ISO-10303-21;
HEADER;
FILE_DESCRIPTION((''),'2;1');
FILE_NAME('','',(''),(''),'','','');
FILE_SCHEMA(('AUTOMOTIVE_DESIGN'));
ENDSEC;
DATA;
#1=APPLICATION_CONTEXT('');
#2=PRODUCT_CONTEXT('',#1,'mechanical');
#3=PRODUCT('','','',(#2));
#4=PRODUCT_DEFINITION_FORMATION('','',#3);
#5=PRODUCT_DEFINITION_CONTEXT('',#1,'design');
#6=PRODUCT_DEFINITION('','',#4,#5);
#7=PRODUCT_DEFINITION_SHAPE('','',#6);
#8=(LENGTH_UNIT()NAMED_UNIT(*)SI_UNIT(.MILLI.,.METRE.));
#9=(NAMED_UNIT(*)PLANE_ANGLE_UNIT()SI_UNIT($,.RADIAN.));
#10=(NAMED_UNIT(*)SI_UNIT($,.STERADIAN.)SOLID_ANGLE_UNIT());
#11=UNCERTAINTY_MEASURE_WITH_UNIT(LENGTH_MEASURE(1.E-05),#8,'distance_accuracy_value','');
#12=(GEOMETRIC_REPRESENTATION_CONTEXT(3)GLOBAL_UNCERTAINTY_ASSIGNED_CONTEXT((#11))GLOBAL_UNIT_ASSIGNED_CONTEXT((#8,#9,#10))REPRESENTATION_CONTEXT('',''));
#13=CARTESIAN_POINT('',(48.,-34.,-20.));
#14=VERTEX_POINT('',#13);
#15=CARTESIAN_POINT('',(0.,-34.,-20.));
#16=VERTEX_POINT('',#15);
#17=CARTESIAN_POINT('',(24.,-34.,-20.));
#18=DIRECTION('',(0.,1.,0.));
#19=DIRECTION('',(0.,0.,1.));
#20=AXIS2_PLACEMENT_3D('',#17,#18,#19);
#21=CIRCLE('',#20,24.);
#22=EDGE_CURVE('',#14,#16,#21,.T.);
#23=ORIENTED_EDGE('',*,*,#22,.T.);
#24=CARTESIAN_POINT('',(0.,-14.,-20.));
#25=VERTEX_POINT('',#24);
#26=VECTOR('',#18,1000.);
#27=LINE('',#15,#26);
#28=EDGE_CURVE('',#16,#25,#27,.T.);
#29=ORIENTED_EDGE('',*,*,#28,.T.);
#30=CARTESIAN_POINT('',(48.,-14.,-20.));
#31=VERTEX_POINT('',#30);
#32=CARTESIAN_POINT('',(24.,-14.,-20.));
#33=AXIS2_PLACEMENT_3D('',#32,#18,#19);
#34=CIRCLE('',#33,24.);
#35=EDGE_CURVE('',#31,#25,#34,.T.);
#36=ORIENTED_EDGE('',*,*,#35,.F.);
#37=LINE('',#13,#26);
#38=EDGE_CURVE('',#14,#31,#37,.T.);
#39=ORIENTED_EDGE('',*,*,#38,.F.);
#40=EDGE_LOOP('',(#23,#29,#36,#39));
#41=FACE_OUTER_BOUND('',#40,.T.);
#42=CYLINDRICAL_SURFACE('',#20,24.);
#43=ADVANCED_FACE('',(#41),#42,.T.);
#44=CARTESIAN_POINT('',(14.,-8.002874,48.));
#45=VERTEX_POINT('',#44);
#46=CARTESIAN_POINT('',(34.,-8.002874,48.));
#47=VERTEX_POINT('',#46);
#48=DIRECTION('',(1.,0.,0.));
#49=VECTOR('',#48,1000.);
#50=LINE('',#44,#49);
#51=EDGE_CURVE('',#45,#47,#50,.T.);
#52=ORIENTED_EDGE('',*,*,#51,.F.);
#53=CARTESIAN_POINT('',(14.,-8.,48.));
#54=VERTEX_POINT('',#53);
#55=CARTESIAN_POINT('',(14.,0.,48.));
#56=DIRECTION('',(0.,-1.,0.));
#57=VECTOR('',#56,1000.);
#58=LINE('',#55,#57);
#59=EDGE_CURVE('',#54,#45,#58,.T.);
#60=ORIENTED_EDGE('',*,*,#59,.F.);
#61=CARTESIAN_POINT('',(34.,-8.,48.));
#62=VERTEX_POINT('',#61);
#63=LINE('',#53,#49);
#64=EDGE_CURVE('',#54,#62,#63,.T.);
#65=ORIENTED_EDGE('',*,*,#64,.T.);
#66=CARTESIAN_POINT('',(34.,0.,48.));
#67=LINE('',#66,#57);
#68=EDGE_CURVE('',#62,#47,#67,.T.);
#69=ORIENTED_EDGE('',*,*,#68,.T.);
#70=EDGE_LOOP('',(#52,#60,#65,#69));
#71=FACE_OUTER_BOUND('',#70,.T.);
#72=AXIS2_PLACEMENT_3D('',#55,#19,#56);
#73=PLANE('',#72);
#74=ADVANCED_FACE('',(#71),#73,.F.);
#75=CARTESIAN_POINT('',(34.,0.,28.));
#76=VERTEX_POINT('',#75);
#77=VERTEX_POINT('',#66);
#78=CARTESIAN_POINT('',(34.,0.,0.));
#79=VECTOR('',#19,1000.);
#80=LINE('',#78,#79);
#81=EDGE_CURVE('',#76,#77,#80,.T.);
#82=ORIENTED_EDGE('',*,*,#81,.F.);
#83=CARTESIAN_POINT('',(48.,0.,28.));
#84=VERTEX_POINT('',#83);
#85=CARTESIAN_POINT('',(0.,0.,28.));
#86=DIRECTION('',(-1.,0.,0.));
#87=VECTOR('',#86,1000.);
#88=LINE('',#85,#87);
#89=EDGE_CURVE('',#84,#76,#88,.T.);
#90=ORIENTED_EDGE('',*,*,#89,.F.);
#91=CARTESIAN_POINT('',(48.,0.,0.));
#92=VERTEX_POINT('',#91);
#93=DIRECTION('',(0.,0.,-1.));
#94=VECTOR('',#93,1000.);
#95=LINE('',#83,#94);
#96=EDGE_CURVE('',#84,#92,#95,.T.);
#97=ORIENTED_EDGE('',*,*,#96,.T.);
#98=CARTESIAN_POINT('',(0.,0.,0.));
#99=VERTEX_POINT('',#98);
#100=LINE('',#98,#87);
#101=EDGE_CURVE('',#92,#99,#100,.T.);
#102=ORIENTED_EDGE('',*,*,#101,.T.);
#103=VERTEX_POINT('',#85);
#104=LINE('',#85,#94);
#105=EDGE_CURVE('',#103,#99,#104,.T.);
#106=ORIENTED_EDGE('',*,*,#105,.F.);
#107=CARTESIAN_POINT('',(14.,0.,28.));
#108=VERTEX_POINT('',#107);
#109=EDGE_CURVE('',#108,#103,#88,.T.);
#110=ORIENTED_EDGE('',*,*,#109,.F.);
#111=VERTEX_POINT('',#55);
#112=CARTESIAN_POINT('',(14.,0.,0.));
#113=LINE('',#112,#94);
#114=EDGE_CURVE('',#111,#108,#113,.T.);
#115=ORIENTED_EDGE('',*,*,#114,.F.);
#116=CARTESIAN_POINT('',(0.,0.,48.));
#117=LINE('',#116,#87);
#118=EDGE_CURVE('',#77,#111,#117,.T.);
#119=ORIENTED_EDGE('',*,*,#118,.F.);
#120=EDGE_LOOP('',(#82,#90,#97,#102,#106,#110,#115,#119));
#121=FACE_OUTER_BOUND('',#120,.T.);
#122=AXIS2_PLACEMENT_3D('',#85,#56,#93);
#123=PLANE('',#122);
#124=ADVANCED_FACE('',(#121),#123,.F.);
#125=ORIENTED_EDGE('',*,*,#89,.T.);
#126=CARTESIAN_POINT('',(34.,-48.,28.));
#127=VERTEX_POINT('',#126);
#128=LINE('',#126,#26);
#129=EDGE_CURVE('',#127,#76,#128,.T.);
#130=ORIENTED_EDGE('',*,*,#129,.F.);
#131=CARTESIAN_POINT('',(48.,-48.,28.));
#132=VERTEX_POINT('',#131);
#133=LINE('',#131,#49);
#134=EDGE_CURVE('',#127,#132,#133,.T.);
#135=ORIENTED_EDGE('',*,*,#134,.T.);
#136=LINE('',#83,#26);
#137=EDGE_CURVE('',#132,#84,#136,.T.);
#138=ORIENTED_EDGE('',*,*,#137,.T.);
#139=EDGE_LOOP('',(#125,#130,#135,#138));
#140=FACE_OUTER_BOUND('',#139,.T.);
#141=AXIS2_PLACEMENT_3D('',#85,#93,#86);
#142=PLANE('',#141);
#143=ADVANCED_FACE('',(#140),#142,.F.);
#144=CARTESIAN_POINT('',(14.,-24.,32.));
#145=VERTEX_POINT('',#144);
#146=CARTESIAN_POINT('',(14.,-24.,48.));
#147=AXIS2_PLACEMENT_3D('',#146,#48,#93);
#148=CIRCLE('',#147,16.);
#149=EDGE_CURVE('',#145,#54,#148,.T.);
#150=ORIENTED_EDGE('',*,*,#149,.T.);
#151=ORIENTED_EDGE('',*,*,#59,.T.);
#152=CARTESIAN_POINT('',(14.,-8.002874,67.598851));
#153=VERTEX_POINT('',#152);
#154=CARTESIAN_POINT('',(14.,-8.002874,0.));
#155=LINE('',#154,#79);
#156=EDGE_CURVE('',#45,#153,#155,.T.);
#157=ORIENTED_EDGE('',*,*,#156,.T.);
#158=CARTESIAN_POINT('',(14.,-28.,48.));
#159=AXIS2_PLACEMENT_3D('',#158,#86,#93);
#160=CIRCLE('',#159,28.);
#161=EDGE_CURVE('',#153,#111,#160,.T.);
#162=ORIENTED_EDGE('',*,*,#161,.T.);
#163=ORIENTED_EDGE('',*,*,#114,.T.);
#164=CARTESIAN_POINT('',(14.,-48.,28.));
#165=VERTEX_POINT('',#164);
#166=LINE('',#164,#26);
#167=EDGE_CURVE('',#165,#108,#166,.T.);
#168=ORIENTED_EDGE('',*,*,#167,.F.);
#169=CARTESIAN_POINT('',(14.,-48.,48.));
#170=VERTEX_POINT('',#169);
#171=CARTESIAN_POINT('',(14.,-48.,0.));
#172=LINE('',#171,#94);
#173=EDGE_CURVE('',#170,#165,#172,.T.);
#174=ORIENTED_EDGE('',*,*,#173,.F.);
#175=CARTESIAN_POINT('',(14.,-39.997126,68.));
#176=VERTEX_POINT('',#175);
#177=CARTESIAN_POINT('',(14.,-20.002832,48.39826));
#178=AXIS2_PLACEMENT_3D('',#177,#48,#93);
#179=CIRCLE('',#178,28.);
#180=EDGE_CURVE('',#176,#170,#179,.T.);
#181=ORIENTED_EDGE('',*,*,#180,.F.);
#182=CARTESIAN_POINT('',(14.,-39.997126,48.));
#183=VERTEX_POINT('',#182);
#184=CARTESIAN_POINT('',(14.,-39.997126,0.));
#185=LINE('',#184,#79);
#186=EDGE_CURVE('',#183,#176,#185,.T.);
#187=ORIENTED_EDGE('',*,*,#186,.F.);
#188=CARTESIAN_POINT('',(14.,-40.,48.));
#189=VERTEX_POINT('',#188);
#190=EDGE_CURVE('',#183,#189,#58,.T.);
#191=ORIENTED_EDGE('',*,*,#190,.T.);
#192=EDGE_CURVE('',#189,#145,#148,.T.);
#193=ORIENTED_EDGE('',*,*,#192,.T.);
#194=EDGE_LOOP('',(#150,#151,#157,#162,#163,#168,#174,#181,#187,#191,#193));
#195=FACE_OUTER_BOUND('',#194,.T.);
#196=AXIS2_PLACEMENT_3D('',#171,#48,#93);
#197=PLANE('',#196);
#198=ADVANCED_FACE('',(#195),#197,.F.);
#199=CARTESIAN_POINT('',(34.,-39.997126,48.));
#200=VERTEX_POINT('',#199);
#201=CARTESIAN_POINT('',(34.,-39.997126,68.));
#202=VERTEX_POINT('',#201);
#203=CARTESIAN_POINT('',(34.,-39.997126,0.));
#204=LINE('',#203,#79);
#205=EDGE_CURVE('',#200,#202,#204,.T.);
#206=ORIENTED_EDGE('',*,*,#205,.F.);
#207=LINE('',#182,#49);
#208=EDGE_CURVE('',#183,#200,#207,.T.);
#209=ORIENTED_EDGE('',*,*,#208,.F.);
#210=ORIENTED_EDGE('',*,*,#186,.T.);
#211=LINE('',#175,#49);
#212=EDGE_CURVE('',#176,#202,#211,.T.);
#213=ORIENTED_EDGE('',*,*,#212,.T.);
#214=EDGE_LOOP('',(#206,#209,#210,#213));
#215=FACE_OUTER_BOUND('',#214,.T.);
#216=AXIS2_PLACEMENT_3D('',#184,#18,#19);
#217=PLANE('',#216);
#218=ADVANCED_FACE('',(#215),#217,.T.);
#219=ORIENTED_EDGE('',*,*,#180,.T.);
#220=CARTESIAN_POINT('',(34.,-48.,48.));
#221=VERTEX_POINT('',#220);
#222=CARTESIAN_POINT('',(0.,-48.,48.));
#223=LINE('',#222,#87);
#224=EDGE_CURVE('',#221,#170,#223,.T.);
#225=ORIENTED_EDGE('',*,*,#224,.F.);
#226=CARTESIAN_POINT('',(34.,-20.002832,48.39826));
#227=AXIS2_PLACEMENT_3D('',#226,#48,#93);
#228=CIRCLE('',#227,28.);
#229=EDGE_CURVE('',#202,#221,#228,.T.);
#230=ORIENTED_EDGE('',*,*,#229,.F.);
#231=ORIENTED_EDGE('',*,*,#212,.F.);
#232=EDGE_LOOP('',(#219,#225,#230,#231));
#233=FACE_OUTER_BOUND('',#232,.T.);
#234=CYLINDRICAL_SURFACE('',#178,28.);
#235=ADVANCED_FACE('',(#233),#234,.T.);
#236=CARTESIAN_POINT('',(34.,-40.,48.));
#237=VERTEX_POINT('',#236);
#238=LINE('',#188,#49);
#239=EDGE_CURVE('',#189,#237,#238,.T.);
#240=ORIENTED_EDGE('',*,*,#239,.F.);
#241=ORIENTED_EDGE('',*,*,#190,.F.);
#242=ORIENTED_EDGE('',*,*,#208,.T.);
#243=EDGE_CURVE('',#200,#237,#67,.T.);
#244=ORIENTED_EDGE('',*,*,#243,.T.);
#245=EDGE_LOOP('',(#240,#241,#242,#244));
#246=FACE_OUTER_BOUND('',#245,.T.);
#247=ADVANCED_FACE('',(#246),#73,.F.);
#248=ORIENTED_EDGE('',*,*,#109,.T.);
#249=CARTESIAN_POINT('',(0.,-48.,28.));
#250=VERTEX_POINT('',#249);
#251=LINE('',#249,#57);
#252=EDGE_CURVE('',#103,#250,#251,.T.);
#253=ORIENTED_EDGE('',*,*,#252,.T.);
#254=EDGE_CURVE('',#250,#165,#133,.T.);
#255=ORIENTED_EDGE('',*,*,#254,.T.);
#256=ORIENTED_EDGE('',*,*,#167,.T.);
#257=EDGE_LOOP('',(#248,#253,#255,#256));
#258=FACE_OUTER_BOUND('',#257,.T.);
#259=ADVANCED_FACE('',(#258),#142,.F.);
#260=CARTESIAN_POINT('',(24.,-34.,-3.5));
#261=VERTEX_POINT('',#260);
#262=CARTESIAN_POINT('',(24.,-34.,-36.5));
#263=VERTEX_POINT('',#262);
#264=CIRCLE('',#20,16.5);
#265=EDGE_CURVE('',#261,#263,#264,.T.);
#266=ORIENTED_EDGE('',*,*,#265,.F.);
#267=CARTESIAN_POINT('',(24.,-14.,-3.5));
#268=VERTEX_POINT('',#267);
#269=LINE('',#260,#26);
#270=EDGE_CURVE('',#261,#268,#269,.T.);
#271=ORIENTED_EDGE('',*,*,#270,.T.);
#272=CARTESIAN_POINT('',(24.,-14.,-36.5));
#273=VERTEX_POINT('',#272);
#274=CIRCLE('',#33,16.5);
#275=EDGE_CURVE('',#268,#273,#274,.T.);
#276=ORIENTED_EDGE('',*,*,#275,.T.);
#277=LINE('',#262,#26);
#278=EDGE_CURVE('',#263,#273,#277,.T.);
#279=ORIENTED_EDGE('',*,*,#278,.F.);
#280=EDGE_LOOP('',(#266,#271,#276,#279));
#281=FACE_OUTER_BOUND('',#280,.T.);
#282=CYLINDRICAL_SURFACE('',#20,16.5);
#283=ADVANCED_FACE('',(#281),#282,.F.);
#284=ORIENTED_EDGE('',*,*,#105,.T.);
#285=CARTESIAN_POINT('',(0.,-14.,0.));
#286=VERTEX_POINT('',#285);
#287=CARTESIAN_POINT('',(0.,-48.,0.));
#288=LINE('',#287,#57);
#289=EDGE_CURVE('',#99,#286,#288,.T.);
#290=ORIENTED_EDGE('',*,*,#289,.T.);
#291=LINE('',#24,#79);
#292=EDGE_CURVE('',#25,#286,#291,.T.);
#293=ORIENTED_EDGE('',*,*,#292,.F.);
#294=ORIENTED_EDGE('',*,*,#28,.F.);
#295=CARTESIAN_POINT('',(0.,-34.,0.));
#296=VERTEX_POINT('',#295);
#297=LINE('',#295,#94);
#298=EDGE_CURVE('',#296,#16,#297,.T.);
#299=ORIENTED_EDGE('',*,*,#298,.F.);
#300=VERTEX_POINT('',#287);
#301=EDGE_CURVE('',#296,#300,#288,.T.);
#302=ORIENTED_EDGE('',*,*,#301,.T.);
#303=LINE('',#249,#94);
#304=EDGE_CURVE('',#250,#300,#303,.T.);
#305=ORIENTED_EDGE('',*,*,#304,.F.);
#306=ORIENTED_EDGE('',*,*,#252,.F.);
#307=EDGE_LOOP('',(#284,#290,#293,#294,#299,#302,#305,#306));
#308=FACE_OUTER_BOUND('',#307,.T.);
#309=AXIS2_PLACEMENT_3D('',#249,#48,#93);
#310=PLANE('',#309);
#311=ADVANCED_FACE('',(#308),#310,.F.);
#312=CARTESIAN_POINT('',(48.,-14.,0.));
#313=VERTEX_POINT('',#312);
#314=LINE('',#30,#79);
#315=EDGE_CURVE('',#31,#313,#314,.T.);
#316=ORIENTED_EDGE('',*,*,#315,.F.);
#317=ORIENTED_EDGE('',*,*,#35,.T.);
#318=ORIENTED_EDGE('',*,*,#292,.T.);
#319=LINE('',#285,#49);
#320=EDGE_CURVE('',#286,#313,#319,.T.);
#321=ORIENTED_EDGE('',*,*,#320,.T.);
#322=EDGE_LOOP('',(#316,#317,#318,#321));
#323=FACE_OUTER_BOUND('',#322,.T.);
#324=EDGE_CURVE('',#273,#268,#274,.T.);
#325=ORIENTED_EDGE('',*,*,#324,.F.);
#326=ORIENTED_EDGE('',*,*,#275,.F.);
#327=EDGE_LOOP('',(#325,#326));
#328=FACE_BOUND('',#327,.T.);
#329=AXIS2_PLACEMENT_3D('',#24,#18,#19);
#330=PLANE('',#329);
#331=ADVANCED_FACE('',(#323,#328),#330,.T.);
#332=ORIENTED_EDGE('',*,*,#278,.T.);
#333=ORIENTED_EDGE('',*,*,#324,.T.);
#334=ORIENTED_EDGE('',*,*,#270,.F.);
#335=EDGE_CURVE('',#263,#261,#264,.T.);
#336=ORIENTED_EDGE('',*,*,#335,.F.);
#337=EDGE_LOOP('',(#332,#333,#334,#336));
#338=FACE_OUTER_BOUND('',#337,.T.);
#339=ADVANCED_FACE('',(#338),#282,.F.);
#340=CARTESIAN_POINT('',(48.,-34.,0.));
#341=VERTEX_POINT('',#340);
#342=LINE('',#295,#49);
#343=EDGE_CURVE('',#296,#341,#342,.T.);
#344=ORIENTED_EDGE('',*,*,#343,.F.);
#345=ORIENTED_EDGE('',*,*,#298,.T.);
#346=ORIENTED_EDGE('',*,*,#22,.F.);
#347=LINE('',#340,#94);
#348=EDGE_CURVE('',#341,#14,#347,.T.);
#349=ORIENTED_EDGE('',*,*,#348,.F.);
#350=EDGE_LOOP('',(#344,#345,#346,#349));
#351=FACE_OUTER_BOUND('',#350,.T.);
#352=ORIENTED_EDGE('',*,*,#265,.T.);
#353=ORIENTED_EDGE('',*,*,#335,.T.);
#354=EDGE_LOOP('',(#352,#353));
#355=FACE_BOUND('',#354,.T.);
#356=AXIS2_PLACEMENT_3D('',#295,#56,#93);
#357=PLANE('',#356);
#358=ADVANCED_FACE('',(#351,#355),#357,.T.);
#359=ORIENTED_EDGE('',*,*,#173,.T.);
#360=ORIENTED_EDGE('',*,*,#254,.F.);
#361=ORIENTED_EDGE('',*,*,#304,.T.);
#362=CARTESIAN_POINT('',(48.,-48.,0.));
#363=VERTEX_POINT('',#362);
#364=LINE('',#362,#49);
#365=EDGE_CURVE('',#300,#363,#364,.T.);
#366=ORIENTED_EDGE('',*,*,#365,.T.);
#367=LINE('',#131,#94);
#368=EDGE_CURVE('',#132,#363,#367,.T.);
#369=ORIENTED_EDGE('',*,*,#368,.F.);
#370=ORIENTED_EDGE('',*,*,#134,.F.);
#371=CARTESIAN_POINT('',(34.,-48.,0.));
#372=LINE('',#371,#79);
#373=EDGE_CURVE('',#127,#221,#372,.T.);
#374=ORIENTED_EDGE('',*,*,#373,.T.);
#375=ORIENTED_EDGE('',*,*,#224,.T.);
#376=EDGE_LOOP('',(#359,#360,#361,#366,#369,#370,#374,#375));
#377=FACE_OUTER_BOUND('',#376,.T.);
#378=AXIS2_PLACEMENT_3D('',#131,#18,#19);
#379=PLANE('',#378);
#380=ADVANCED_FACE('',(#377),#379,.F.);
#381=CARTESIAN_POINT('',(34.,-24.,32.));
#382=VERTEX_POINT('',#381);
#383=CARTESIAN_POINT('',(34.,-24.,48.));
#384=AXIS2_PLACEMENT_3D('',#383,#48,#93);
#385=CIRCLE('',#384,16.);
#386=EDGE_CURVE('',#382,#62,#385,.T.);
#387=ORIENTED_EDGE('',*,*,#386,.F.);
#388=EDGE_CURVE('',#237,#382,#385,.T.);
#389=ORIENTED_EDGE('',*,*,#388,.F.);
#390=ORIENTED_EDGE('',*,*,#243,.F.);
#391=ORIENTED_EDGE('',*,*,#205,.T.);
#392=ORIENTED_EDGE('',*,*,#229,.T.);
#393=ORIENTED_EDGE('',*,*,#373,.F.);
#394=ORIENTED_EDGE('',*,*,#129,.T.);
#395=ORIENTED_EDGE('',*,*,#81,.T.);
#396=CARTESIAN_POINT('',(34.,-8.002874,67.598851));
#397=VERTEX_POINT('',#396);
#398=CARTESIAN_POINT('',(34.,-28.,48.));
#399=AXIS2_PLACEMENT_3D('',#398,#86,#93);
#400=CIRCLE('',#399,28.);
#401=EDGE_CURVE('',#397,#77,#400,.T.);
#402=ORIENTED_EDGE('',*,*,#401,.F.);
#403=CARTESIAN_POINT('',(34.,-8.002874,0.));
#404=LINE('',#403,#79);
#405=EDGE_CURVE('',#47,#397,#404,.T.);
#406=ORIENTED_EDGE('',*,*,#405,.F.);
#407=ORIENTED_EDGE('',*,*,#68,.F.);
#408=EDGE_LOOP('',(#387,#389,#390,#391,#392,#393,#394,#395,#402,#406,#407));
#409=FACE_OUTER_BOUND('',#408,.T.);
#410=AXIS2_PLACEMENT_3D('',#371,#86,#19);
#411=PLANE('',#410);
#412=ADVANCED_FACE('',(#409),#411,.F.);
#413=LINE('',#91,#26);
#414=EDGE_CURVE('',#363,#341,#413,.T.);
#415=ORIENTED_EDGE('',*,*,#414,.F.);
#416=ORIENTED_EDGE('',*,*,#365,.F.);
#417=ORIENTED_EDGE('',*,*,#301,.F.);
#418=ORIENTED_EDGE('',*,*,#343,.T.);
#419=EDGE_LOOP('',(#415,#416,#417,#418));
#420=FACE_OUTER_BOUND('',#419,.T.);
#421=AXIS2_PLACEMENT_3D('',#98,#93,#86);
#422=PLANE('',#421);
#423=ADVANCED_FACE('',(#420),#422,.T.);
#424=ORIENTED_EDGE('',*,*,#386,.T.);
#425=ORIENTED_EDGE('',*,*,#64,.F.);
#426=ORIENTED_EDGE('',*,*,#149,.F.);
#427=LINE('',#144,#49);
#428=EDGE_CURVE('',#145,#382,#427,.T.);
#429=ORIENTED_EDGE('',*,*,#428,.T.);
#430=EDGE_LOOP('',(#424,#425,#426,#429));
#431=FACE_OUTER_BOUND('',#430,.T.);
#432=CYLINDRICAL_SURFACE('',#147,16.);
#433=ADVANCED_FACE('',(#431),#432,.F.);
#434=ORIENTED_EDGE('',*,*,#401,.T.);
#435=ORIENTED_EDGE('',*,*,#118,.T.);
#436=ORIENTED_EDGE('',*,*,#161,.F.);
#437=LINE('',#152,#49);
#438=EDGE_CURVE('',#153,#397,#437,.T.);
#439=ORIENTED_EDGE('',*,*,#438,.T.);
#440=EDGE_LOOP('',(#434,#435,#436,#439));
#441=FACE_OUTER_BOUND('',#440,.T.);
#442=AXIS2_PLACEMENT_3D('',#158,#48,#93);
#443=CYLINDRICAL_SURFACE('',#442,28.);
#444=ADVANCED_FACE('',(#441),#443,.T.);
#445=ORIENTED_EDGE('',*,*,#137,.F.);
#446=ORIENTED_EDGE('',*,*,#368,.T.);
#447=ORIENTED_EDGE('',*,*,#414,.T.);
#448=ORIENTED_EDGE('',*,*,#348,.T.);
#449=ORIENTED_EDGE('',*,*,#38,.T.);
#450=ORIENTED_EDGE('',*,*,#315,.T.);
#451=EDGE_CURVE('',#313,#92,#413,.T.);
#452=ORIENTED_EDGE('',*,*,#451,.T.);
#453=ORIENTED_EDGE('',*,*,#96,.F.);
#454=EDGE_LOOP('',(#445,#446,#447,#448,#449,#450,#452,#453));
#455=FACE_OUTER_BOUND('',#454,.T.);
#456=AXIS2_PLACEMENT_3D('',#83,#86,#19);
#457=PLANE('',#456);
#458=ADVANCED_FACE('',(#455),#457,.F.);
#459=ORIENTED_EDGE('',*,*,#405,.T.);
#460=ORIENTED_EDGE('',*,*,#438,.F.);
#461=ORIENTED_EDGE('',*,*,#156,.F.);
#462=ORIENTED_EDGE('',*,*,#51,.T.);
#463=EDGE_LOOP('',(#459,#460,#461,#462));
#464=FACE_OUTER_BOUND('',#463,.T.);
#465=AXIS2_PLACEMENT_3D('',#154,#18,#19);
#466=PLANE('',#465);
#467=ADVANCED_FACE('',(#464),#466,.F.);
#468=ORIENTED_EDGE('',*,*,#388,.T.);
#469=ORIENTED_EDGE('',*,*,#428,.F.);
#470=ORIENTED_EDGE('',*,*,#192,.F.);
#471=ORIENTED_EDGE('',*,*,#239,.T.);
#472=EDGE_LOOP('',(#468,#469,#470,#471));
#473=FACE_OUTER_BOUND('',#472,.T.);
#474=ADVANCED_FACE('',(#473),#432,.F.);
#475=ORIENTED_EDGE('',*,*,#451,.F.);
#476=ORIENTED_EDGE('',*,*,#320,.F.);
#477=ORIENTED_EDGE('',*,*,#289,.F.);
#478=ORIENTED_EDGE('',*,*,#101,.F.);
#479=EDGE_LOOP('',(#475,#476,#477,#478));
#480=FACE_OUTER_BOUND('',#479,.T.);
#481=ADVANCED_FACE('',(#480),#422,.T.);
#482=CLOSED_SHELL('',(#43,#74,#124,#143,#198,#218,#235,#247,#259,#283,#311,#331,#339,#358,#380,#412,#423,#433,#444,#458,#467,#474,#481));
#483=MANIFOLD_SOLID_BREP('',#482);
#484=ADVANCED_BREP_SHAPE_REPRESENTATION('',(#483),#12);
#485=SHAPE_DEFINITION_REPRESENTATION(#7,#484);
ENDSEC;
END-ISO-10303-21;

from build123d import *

# Parameters (mm, degrees)
BASE_BLOCK_SKETCH_W = 48
BASE_BLOCK_SKETCH_H = 48
BASE_BLOCK_DEPTH    = 28
HOOK_ARM_DEPTH      = 48
EYE_ARM_DEPTH       = 48
EYE_BOSS_DEPTH      = 20
EYE_BORE_SKETCH_R   = 16.5
EYE_BORE_33_DEPTH   = 20
HOOK_END_DEPTH      = 20
HOOK_SLOT_32_DEPTH  = 20


with BuildPart() as part:
    # Base Block Sketch → Base Block (new body)
    with BuildSketch(Plane.XY):
        with Locations((24, -24)):
            Rectangle(BASE_BLOCK_SKETCH_W, BASE_BLOCK_SKETCH_H)
    extrude(amount=BASE_BLOCK_DEPTH)

    # Hook Arm Sketch → Hook Arm (add)
    with BuildSketch(Plane(origin=(0, 0, 0), x_dir=(1, 0, 0), z_dir=(0, 1, 0))):
        Polygon((34, -28), (24, -28), (14, -28), (14, -48), (34, -48), align=None)
    extrude(amount=-HOOK_ARM_DEPTH)

    # Eye Arm Sketch → Eye Arm (add)
    with BuildSketch(Plane(origin=(48, 0, 0), x_dir=(0, 0, -1), z_dir=(1, 0, 0))):
        Polygon((0, -24), (0, -14), (20, -14), (20, -34), (0, -34), align=None)
    extrude(amount=-EYE_ARM_DEPTH)

    # Eye Boss Sketch → Eye Boss (add)
    with BuildSketch(Plane(origin=(0, -14, 0), x_dir=(1, 0, 0), z_dir=(0, 1, 0))):
        with BuildLine():
            Line((0, 20), (48, 20))
            ThreePointArc((48, 20), (24, 44), (0, 20))
        make_face()
    extrude(amount=-EYE_BOSS_DEPTH)

    # Eye Bore Sketch → Eye Bore Ø33 (cut)
    with BuildSketch(Plane(origin=(0, -14, 0), x_dir=(1, 0, 0), z_dir=(0, 1, 0))):
        with Locations(Location((24, 20, 0), (0, 0, 270))):
            Circle(EYE_BORE_SKETCH_R)
    extrude(amount=-EYE_BORE_33_DEPTH, mode=Mode.SUBTRACT)

    # Hook End Sketch → Hook End (add)
    with BuildSketch(Plane(origin=(34, 0, 0), x_dir=(0, 0, -1), z_dir=(1, 0, 0))):
        with BuildLine():
            Line((-67.598850506, -8.002873735), (-48, -8.002873735))
            Line((-48, -8.002873735), (-48, 0))
            ThreePointArc((-48, 0), (-58.584905871, -2.077813215), (-67.598850506, -8.002873735))
        make_face()
        with BuildLine():
            Line((-48, -48), (-48, -39.997126265))
            Line((-48, -39.997126265), (-68, -39.997126265))
            ThreePointArc((-68, -39.997126265), (-58.800418806, -45.998891596), (-48, -48))
        make_face()
    extrude(amount=-HOOK_END_DEPTH)

    # Hook Slot Sketch → Hook Slot 32 (cut)
    with BuildSketch(Plane(origin=(34, 0, 0), x_dir=(0, 0, -1), z_dir=(1, 0, 0))):
        with BuildLine():
            Line((-48, -8), (-48, -8.002873735))
            Line((-48, -8.002873735), (-48, -39.997126265))
            Line((-48, -39.997126265), (-48, -40))
            ThreePointArc((-48, -40), (-32, -24), (-48, -8))
        make_face()
    extrude(amount=-HOOK_SLOT_32_DEPTH, mode=Mode.SUBTRACT)


solid = part.part
